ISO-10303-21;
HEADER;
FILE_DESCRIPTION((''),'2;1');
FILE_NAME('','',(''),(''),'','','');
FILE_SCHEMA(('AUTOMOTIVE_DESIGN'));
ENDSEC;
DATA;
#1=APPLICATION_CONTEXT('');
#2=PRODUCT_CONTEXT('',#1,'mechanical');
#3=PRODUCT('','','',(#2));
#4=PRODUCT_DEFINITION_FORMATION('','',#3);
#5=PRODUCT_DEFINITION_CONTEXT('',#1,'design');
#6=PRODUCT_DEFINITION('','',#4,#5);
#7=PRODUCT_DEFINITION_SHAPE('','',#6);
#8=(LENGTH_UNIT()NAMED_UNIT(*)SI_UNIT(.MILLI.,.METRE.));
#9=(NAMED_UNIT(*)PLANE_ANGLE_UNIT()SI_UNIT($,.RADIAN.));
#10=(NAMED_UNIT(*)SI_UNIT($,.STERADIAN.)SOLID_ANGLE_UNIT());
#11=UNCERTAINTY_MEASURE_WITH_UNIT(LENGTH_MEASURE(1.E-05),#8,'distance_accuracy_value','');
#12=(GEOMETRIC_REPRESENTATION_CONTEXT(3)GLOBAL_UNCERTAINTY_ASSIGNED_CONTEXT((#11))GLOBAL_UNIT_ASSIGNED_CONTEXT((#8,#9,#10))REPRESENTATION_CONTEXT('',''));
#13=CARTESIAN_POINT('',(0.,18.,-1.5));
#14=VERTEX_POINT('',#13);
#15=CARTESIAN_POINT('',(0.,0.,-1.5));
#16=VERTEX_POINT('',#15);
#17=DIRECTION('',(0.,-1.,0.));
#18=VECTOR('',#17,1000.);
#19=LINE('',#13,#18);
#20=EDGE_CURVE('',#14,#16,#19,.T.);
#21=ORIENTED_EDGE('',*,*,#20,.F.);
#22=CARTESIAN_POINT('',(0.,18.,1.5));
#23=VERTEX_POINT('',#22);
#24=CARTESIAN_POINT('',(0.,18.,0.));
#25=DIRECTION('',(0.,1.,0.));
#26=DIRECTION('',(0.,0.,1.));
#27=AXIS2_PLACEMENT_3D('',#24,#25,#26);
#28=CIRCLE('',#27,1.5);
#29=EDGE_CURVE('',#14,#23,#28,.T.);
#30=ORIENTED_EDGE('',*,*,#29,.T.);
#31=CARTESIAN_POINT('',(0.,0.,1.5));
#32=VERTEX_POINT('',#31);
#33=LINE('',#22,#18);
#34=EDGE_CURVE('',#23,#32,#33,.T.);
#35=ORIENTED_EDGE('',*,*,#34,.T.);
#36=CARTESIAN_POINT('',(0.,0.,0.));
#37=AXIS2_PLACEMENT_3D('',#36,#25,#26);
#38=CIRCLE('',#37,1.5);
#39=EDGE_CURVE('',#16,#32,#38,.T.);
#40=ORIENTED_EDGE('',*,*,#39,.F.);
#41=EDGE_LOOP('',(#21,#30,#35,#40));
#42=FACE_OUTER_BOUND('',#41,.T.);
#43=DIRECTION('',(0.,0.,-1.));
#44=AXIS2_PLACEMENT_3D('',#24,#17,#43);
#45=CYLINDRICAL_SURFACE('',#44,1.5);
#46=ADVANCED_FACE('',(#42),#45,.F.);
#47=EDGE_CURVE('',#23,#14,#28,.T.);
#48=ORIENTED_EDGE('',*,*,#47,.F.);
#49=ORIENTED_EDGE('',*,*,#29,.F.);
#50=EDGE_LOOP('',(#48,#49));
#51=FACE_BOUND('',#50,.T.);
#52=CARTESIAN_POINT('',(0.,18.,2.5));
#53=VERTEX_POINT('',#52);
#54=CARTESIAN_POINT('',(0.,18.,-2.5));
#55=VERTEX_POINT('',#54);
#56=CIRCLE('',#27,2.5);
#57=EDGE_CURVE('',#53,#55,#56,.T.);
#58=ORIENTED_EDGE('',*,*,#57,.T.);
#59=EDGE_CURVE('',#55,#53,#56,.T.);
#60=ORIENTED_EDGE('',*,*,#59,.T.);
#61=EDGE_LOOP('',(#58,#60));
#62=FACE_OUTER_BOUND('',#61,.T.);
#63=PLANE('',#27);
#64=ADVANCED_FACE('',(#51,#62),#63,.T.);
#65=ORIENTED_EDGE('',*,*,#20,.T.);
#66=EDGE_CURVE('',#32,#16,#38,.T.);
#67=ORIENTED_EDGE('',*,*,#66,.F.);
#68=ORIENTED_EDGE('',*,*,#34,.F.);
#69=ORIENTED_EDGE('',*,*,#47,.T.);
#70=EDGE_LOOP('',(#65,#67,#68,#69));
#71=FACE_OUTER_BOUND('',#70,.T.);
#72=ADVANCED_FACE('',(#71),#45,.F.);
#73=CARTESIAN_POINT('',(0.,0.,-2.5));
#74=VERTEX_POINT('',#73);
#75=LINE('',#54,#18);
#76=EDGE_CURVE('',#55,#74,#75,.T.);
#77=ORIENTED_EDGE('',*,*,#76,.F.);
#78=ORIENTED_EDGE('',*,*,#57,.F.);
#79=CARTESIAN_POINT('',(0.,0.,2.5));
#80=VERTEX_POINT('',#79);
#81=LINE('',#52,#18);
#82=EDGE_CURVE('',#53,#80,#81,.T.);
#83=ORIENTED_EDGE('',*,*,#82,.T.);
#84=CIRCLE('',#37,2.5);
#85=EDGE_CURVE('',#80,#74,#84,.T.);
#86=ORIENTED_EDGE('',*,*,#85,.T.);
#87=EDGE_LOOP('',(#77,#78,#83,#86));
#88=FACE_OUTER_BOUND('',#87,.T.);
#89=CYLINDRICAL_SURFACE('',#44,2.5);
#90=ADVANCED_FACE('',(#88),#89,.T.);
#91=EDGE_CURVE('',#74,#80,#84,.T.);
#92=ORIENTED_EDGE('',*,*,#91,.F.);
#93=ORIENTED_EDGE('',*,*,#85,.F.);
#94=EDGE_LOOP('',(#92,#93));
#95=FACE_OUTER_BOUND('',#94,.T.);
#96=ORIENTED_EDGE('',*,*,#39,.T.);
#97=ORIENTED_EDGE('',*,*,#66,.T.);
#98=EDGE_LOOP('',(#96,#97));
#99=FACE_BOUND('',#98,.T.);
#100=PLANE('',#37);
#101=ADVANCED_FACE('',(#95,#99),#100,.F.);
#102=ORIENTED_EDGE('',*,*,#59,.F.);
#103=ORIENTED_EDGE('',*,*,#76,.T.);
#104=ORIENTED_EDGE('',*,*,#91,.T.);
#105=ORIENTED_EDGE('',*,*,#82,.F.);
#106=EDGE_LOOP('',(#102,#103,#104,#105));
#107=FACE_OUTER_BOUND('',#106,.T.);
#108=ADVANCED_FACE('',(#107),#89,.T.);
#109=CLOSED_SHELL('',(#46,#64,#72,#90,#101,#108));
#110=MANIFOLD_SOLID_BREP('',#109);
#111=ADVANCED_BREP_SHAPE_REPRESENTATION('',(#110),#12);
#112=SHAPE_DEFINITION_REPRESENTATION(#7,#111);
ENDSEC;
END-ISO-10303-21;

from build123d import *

# Parameters (mm, degrees)
SKETCH_1_R      = 2.5
SKETCH_1_R_2    = 1.5
EXTRUDE_1_DEPTH = 18


with BuildPart() as part:
    # 草图1 → 凸台-拉伸1 (new body)
    with BuildSketch(Plane(origin=(0, 0, 0), x_dir=(1, 0, 0), z_dir=(0, 1, 0))):
        with Locations(Location((0, 0, 0), (0, 0, 270))):
            Circle(SKETCH_1_R)
        with Locations(Location((0, 0, 0), (0, 0, 270))):
            Circle(SKETCH_1_R_2, mode=Mode.SUBTRACT)
    extrude(amount=EXTRUDE_1_DEPTH)


solid = part.part
